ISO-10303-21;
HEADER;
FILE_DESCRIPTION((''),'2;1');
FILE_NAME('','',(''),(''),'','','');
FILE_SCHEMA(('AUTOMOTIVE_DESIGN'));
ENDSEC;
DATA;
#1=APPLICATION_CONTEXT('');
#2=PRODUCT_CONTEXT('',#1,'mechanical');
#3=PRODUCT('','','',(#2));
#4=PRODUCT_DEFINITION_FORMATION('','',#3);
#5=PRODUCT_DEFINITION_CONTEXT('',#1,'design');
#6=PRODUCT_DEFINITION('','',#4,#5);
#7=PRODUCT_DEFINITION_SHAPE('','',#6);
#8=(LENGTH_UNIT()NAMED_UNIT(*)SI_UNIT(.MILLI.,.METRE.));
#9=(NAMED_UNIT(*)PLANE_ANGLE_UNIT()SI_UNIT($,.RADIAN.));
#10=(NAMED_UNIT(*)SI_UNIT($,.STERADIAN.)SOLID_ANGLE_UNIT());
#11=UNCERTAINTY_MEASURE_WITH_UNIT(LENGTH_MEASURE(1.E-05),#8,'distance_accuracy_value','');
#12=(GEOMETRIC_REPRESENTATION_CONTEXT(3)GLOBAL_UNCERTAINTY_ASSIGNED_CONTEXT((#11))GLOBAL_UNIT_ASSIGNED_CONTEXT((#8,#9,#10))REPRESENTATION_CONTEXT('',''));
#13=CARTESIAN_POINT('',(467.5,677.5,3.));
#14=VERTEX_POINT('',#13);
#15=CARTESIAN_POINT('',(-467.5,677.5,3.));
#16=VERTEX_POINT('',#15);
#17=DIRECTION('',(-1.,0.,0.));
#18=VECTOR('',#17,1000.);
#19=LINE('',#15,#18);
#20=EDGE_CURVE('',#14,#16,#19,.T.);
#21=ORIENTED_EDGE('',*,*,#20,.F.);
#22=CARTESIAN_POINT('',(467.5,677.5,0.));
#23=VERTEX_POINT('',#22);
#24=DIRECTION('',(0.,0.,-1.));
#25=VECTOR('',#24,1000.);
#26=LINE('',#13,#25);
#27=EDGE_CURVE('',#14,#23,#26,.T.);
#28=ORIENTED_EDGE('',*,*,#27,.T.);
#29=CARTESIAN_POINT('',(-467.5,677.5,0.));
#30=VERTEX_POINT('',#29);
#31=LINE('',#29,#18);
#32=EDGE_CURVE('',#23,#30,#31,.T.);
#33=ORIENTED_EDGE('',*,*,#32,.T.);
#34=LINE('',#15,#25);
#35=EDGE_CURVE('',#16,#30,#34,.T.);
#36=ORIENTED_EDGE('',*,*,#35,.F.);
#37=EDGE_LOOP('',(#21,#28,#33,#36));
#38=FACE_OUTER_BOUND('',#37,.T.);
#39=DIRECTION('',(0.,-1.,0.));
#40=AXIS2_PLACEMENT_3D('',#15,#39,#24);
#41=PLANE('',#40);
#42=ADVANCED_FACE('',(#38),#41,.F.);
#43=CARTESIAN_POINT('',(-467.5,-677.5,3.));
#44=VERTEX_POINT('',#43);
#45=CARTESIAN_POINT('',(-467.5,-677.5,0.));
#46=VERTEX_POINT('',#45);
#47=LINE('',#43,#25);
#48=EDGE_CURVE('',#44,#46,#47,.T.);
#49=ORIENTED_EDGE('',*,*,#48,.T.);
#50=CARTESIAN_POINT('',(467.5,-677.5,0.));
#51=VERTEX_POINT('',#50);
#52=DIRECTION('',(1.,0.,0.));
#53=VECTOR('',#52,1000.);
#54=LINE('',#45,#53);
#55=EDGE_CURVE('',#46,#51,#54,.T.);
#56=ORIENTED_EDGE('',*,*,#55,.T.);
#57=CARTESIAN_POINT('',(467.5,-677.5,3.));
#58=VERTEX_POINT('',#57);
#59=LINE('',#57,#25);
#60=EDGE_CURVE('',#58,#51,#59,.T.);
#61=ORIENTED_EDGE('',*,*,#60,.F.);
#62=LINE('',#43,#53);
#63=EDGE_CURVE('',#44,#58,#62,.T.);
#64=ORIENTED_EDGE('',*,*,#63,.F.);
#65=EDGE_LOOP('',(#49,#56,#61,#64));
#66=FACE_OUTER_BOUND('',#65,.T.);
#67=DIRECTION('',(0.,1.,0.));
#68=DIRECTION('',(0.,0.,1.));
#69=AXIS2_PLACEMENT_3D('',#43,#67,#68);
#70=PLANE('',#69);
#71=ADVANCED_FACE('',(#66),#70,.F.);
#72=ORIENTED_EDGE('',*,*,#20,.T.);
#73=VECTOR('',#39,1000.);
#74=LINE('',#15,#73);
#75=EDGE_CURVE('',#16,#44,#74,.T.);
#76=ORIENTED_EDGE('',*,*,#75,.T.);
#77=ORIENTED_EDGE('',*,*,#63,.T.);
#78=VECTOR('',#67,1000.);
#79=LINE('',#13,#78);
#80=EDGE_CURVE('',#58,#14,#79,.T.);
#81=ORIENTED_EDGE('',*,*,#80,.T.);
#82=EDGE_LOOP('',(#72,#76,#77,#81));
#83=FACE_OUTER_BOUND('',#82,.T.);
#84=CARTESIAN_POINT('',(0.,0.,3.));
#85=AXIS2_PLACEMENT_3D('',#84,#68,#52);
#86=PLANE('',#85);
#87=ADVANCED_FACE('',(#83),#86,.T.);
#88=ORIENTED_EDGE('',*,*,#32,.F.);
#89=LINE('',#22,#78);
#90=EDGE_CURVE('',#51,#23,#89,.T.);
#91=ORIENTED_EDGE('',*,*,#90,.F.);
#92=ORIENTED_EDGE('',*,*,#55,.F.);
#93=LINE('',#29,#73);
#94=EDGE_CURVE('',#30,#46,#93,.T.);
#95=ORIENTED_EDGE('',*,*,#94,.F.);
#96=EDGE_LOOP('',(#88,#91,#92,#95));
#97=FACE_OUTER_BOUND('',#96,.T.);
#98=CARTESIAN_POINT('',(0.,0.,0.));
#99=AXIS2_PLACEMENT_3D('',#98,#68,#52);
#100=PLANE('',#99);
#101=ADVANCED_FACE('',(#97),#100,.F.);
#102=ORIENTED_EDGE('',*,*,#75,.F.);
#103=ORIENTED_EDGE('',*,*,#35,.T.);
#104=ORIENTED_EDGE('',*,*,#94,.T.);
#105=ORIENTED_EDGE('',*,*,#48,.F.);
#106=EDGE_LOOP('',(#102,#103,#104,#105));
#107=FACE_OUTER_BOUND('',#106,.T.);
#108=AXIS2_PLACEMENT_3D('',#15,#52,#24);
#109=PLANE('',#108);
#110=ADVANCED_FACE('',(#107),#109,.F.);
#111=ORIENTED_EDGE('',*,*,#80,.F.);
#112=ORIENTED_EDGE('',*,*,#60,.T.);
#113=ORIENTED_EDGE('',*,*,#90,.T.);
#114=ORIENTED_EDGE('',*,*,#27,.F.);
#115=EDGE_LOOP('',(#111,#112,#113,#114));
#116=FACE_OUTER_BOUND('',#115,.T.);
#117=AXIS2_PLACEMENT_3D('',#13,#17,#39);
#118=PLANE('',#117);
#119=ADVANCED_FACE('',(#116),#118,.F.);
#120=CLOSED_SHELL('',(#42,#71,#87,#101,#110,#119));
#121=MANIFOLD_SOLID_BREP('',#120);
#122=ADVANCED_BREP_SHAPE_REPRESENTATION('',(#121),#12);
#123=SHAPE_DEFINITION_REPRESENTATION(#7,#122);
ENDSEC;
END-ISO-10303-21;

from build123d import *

# Parameters (mm, degrees)
SKETCH_1_W      = 935
SKETCH_1_H      = 1355
EXTRUDE_1_DEPTH = 3


with BuildPart() as part:
    # 草图1 → 凸台-拉伸1 (new body)
    with BuildSketch(Plane.XY):
        Rectangle(SKETCH_1_W, SKETCH_1_H)
    extrude(amount=EXTRUDE_1_DEPTH)


solid = part.part
